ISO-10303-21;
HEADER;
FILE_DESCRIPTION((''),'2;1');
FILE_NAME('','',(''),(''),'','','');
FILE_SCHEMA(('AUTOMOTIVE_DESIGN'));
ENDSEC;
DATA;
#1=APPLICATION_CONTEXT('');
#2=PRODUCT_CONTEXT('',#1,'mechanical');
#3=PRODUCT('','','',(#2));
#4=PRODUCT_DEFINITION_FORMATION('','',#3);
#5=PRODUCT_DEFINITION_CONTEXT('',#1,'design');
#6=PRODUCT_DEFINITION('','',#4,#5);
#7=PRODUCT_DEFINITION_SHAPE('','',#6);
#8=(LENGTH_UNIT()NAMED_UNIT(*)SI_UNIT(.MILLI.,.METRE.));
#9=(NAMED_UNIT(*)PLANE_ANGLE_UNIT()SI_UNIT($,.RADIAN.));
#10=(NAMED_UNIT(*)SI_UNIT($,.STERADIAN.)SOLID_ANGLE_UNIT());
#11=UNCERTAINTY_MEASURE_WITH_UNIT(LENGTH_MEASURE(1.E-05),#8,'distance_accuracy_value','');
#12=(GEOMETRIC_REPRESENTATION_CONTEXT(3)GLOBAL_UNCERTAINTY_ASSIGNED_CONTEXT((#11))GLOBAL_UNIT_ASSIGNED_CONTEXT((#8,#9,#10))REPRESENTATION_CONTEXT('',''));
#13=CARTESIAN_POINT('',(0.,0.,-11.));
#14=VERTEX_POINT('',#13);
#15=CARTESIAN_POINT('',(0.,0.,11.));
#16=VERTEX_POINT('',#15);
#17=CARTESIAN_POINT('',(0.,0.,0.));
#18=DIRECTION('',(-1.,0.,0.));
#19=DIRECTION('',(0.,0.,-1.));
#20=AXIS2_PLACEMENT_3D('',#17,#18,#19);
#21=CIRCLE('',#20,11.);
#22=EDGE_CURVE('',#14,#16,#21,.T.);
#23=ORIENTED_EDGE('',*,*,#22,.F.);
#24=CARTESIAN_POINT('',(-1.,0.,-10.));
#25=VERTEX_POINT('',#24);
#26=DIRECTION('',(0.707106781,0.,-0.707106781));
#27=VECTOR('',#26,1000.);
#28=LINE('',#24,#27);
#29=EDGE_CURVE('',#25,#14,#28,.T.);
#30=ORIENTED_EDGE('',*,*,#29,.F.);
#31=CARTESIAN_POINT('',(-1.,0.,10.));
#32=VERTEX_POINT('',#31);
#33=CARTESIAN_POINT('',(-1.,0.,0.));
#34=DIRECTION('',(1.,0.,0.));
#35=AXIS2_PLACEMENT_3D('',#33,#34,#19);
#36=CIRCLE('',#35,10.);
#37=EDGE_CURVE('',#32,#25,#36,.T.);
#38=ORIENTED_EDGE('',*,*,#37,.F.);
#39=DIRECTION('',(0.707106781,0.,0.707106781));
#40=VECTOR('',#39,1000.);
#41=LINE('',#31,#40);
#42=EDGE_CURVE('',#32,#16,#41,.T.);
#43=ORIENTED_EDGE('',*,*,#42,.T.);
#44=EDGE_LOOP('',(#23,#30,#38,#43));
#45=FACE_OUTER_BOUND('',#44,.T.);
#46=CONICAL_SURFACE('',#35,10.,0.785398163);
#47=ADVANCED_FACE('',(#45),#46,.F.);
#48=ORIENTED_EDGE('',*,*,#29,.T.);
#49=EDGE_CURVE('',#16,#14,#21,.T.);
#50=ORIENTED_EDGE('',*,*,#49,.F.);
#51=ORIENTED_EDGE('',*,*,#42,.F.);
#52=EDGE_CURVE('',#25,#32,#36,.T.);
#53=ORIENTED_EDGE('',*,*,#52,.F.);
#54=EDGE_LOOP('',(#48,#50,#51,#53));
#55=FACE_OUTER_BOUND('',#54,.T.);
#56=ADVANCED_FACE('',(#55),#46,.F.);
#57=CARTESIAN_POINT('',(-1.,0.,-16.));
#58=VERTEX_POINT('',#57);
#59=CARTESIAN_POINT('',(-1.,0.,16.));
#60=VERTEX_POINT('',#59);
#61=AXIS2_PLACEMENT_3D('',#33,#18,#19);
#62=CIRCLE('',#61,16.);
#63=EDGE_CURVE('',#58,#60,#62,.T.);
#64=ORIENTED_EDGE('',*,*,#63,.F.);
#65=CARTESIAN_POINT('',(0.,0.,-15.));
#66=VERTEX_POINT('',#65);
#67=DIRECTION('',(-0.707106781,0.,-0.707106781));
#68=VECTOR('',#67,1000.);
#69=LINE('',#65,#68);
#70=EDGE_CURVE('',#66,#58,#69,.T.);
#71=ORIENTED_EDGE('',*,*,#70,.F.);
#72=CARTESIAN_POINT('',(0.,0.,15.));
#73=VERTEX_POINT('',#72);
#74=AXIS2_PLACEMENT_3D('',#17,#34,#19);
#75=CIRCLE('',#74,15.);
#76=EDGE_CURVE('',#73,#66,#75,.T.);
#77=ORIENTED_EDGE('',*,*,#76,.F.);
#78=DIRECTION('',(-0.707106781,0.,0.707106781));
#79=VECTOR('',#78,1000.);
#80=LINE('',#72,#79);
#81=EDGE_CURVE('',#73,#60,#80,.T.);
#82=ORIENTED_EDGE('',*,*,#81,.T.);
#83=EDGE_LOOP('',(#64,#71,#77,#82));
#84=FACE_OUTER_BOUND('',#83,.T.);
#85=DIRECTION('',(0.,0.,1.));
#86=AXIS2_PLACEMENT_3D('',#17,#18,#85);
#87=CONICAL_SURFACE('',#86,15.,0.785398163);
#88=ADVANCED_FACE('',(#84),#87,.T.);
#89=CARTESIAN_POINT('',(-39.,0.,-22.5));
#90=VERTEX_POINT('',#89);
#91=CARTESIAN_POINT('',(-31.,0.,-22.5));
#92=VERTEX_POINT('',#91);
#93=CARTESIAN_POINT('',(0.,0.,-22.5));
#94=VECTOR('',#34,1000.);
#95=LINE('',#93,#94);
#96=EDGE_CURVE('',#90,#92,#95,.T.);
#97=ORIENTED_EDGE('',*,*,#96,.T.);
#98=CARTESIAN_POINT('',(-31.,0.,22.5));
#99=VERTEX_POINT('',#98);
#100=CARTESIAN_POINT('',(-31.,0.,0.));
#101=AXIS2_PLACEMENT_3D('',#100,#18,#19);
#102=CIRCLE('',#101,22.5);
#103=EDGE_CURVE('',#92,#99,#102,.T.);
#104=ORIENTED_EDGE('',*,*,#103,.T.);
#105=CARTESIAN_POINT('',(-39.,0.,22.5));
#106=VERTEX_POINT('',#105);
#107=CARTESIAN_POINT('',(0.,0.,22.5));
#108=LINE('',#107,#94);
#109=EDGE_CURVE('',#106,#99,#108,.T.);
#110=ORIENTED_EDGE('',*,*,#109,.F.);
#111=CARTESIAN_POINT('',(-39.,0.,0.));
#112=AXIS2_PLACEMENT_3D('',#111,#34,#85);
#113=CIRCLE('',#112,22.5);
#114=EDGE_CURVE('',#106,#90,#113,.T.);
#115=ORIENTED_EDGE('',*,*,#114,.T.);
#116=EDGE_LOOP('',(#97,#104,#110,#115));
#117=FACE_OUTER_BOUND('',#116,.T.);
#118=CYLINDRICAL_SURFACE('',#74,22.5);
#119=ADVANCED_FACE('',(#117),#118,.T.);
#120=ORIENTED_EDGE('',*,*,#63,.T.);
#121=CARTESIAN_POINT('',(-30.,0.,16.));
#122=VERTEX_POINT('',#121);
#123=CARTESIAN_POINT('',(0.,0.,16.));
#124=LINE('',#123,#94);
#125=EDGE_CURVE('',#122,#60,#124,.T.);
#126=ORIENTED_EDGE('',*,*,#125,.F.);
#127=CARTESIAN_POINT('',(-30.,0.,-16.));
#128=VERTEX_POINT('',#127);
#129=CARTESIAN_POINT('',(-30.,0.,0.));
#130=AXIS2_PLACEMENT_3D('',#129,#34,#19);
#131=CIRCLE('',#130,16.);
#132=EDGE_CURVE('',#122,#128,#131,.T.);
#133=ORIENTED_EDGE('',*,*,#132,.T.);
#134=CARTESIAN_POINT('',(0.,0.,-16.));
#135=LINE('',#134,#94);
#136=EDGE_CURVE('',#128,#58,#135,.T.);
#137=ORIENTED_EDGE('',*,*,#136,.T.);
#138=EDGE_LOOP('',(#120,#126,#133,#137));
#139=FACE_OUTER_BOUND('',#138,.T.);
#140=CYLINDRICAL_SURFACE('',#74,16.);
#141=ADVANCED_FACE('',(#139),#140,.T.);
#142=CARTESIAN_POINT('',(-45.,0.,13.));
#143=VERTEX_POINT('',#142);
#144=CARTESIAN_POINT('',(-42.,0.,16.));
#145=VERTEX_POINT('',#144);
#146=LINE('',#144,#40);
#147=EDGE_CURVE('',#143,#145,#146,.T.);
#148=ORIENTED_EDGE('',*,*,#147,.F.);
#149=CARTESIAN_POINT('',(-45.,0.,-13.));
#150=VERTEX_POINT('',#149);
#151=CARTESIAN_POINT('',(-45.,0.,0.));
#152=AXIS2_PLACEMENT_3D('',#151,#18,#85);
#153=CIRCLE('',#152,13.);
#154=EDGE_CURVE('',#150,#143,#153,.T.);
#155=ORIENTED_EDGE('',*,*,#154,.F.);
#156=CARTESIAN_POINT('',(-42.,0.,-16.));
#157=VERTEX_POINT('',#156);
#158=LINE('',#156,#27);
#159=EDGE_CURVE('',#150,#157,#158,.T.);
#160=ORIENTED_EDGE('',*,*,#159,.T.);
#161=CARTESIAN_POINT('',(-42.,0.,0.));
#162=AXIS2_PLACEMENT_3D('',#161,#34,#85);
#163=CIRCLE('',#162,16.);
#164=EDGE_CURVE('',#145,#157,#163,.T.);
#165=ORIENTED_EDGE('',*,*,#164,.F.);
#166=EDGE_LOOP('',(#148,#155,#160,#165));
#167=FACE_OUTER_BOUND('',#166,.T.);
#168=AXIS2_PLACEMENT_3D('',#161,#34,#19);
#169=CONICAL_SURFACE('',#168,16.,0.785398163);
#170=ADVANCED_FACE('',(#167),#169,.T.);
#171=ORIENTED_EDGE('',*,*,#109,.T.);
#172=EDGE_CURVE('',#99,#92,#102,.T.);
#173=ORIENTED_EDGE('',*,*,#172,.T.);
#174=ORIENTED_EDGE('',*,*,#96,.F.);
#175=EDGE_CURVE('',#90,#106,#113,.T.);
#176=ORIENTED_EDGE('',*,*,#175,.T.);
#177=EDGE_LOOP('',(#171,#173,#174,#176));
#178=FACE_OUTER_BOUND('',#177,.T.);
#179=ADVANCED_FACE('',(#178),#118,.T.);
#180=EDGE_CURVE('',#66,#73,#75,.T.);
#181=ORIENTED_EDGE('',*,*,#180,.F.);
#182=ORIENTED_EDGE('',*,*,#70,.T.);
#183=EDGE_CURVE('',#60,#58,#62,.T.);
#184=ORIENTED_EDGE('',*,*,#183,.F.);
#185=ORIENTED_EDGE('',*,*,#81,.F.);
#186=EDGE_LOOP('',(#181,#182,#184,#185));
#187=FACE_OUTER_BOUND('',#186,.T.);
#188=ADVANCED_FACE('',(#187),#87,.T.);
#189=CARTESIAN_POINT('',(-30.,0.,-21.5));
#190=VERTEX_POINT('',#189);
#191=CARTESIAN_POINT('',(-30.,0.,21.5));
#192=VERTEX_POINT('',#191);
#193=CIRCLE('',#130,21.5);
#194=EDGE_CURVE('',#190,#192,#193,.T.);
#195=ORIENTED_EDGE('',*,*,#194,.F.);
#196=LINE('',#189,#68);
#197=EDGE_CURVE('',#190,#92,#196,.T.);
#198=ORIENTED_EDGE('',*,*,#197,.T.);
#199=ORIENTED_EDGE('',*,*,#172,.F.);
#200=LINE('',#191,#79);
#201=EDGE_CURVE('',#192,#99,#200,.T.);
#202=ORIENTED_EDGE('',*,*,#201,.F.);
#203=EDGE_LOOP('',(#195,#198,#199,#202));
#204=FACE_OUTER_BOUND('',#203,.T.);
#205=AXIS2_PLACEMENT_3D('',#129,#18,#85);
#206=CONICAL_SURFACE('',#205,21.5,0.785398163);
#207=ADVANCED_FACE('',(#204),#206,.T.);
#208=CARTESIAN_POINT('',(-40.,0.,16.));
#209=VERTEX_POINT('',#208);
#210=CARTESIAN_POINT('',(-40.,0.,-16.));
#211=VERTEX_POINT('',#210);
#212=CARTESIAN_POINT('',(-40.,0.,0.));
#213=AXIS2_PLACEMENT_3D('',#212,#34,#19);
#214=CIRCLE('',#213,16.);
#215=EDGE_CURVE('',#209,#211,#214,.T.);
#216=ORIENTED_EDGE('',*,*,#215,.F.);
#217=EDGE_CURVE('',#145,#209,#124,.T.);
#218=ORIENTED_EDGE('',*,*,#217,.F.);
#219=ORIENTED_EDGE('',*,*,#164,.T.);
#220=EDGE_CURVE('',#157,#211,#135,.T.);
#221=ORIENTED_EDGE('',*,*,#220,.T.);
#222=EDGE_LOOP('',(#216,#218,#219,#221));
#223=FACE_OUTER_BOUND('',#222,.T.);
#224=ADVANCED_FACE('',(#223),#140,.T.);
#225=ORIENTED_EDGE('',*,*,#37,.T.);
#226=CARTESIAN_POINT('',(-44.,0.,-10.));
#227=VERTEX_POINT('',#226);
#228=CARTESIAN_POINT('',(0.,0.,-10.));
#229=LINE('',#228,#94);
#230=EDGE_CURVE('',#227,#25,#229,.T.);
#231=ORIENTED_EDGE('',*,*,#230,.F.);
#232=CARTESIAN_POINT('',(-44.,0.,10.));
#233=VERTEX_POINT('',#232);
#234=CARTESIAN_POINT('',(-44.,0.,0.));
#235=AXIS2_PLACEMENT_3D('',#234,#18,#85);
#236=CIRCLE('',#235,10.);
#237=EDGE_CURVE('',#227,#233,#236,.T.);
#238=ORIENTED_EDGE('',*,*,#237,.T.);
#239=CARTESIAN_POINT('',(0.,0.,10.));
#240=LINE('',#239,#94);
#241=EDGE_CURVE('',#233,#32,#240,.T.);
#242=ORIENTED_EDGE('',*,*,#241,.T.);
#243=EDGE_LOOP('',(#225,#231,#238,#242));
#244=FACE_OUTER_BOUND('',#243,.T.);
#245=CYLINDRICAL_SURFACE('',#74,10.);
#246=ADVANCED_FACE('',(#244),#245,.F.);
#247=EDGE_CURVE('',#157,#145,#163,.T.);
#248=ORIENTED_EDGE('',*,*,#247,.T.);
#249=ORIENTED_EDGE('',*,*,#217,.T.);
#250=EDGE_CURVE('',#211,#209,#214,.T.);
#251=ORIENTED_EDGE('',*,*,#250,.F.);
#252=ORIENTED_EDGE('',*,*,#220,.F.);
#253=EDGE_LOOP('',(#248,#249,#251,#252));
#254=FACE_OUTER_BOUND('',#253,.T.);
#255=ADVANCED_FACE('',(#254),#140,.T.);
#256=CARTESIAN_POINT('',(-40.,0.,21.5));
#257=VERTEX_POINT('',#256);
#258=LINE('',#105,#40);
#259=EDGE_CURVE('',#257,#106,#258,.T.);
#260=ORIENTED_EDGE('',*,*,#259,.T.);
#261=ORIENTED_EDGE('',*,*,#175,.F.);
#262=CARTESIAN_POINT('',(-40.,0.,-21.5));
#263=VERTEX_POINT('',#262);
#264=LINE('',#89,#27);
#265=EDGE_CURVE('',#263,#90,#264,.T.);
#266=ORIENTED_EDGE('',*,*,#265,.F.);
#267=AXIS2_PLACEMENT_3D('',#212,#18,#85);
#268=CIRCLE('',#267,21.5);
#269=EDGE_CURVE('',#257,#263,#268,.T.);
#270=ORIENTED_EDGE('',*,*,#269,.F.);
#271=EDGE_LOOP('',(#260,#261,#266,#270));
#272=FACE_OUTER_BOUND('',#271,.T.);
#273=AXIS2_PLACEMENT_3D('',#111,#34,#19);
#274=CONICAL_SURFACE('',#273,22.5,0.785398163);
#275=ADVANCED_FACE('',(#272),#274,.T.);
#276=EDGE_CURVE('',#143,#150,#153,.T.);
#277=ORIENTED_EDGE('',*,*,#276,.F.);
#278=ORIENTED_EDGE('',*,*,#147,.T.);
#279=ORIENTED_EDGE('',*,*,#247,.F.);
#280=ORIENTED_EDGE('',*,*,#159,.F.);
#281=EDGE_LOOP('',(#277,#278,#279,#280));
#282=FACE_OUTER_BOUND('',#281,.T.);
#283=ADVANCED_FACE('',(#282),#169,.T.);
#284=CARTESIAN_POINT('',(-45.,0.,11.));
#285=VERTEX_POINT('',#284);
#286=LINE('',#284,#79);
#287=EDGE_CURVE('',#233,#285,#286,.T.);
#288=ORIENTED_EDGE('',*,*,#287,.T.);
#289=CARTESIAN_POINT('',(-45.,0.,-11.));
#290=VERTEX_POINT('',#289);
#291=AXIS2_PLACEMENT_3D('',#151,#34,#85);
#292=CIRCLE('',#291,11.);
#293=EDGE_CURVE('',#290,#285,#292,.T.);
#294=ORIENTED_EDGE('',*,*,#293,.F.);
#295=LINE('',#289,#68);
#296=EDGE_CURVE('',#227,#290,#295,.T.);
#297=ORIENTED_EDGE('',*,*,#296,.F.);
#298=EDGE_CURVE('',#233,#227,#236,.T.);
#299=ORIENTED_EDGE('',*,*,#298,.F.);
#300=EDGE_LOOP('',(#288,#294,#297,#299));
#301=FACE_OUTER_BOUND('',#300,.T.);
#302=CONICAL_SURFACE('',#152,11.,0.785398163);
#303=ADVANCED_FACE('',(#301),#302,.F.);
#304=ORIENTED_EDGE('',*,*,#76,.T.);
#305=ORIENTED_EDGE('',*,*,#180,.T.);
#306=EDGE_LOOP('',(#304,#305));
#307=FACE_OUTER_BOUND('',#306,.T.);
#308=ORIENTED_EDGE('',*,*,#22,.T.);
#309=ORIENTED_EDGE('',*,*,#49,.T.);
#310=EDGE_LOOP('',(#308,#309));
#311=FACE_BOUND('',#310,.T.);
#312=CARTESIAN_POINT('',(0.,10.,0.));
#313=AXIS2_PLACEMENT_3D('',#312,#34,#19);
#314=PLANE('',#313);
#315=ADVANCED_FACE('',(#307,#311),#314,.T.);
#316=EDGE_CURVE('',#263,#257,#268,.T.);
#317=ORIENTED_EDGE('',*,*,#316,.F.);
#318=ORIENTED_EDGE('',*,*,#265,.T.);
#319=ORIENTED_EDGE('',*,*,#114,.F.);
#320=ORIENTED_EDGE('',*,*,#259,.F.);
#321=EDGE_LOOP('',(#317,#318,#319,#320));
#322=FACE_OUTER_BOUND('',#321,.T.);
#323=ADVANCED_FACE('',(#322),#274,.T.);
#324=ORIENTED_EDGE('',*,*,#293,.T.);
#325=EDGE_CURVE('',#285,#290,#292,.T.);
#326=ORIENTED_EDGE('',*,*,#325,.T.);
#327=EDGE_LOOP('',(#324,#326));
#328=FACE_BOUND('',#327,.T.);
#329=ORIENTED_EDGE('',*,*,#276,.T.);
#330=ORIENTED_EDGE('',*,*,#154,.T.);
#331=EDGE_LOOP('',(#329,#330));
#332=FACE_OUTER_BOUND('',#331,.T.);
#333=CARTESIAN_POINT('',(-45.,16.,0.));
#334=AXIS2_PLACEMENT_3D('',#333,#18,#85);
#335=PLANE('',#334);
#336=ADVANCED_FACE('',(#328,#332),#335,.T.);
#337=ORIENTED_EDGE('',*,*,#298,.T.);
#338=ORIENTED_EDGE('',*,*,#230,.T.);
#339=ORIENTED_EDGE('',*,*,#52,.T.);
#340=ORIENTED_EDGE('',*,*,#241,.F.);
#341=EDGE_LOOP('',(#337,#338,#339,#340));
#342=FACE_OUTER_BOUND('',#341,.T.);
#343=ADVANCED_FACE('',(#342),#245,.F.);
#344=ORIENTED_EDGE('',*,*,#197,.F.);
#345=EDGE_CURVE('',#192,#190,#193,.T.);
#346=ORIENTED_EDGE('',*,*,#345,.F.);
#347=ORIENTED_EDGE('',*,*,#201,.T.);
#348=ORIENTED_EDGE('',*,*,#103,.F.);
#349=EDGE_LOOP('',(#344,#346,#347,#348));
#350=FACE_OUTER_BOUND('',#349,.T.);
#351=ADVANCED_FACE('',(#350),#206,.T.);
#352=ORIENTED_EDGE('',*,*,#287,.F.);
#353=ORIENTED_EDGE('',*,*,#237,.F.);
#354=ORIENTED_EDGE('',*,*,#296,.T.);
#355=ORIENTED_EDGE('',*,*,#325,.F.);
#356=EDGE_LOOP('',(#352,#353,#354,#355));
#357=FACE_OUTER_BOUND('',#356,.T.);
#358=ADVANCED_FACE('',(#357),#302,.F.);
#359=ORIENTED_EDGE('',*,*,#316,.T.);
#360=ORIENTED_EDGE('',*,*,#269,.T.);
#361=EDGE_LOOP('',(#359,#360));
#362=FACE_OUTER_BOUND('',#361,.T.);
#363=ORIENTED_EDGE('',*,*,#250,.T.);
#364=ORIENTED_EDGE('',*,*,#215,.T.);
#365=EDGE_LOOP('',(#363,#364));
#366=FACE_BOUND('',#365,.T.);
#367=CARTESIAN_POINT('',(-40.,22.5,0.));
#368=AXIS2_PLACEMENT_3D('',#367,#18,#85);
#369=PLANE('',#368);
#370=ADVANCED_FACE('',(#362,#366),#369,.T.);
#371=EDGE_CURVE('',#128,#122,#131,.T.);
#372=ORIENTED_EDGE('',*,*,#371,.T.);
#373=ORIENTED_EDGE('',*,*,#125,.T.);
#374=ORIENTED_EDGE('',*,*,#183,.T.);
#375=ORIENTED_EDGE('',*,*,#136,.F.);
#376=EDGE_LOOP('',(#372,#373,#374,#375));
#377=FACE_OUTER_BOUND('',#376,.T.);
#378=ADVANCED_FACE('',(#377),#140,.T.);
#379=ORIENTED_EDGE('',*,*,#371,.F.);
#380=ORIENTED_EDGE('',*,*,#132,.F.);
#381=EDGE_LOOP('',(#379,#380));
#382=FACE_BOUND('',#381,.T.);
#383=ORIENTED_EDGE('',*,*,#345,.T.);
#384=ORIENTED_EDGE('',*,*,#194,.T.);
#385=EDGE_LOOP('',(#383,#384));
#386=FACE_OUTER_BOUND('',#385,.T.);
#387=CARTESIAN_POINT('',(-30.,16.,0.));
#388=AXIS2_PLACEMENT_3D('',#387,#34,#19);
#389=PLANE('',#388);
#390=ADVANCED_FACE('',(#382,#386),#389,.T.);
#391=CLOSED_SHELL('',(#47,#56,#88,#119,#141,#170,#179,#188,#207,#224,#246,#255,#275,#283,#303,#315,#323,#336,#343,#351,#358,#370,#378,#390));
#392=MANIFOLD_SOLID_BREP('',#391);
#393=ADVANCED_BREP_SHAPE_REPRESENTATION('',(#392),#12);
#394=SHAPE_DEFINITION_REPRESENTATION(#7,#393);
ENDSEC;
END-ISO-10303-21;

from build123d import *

# Parameters (mm, degrees)
CHAMFER1_SIZE = 1
CHAMFER2_SIZE = 3


with BuildPart() as part:
    # Sketch2 → Revolve1 (revolve)
    with BuildSketch(Plane.XY, mode=Mode.PRIVATE) as revolve1_sk:
        Polygon((0, 10), (0, 16), (-30, 16), (-30, 22.5), (-40, 22.5), (-40, 16), (-45, 16), (-45, 10), align=None)
    revolve(revolve1_sk.sketch.rotate(Axis((0, 0, 0), (-1, 0, 0)), 90), axis=Axis((0, 0, 0), (-1, 0, 0)))

    # Chamfer1
    chamfer1_edges = [part.edges().sort_by_distance(p)[0] for p in [
        (0, 0, 16),
        (-30, 0, 22.5),
        (-40, 0, 22.5),
        (-45, 0, 10),
        (0, 0, 10),
    ]]
    chamfer(chamfer1_edges, length=CHAMFER1_SIZE)

    # Chamfer2
    chamfer2_edges = [part.edges().sort_by_distance(p)[0] for p in [
        (-45, 0, 16),
    ]]
    chamfer(chamfer2_edges, length=CHAMFER2_SIZE)


solid = part.part
